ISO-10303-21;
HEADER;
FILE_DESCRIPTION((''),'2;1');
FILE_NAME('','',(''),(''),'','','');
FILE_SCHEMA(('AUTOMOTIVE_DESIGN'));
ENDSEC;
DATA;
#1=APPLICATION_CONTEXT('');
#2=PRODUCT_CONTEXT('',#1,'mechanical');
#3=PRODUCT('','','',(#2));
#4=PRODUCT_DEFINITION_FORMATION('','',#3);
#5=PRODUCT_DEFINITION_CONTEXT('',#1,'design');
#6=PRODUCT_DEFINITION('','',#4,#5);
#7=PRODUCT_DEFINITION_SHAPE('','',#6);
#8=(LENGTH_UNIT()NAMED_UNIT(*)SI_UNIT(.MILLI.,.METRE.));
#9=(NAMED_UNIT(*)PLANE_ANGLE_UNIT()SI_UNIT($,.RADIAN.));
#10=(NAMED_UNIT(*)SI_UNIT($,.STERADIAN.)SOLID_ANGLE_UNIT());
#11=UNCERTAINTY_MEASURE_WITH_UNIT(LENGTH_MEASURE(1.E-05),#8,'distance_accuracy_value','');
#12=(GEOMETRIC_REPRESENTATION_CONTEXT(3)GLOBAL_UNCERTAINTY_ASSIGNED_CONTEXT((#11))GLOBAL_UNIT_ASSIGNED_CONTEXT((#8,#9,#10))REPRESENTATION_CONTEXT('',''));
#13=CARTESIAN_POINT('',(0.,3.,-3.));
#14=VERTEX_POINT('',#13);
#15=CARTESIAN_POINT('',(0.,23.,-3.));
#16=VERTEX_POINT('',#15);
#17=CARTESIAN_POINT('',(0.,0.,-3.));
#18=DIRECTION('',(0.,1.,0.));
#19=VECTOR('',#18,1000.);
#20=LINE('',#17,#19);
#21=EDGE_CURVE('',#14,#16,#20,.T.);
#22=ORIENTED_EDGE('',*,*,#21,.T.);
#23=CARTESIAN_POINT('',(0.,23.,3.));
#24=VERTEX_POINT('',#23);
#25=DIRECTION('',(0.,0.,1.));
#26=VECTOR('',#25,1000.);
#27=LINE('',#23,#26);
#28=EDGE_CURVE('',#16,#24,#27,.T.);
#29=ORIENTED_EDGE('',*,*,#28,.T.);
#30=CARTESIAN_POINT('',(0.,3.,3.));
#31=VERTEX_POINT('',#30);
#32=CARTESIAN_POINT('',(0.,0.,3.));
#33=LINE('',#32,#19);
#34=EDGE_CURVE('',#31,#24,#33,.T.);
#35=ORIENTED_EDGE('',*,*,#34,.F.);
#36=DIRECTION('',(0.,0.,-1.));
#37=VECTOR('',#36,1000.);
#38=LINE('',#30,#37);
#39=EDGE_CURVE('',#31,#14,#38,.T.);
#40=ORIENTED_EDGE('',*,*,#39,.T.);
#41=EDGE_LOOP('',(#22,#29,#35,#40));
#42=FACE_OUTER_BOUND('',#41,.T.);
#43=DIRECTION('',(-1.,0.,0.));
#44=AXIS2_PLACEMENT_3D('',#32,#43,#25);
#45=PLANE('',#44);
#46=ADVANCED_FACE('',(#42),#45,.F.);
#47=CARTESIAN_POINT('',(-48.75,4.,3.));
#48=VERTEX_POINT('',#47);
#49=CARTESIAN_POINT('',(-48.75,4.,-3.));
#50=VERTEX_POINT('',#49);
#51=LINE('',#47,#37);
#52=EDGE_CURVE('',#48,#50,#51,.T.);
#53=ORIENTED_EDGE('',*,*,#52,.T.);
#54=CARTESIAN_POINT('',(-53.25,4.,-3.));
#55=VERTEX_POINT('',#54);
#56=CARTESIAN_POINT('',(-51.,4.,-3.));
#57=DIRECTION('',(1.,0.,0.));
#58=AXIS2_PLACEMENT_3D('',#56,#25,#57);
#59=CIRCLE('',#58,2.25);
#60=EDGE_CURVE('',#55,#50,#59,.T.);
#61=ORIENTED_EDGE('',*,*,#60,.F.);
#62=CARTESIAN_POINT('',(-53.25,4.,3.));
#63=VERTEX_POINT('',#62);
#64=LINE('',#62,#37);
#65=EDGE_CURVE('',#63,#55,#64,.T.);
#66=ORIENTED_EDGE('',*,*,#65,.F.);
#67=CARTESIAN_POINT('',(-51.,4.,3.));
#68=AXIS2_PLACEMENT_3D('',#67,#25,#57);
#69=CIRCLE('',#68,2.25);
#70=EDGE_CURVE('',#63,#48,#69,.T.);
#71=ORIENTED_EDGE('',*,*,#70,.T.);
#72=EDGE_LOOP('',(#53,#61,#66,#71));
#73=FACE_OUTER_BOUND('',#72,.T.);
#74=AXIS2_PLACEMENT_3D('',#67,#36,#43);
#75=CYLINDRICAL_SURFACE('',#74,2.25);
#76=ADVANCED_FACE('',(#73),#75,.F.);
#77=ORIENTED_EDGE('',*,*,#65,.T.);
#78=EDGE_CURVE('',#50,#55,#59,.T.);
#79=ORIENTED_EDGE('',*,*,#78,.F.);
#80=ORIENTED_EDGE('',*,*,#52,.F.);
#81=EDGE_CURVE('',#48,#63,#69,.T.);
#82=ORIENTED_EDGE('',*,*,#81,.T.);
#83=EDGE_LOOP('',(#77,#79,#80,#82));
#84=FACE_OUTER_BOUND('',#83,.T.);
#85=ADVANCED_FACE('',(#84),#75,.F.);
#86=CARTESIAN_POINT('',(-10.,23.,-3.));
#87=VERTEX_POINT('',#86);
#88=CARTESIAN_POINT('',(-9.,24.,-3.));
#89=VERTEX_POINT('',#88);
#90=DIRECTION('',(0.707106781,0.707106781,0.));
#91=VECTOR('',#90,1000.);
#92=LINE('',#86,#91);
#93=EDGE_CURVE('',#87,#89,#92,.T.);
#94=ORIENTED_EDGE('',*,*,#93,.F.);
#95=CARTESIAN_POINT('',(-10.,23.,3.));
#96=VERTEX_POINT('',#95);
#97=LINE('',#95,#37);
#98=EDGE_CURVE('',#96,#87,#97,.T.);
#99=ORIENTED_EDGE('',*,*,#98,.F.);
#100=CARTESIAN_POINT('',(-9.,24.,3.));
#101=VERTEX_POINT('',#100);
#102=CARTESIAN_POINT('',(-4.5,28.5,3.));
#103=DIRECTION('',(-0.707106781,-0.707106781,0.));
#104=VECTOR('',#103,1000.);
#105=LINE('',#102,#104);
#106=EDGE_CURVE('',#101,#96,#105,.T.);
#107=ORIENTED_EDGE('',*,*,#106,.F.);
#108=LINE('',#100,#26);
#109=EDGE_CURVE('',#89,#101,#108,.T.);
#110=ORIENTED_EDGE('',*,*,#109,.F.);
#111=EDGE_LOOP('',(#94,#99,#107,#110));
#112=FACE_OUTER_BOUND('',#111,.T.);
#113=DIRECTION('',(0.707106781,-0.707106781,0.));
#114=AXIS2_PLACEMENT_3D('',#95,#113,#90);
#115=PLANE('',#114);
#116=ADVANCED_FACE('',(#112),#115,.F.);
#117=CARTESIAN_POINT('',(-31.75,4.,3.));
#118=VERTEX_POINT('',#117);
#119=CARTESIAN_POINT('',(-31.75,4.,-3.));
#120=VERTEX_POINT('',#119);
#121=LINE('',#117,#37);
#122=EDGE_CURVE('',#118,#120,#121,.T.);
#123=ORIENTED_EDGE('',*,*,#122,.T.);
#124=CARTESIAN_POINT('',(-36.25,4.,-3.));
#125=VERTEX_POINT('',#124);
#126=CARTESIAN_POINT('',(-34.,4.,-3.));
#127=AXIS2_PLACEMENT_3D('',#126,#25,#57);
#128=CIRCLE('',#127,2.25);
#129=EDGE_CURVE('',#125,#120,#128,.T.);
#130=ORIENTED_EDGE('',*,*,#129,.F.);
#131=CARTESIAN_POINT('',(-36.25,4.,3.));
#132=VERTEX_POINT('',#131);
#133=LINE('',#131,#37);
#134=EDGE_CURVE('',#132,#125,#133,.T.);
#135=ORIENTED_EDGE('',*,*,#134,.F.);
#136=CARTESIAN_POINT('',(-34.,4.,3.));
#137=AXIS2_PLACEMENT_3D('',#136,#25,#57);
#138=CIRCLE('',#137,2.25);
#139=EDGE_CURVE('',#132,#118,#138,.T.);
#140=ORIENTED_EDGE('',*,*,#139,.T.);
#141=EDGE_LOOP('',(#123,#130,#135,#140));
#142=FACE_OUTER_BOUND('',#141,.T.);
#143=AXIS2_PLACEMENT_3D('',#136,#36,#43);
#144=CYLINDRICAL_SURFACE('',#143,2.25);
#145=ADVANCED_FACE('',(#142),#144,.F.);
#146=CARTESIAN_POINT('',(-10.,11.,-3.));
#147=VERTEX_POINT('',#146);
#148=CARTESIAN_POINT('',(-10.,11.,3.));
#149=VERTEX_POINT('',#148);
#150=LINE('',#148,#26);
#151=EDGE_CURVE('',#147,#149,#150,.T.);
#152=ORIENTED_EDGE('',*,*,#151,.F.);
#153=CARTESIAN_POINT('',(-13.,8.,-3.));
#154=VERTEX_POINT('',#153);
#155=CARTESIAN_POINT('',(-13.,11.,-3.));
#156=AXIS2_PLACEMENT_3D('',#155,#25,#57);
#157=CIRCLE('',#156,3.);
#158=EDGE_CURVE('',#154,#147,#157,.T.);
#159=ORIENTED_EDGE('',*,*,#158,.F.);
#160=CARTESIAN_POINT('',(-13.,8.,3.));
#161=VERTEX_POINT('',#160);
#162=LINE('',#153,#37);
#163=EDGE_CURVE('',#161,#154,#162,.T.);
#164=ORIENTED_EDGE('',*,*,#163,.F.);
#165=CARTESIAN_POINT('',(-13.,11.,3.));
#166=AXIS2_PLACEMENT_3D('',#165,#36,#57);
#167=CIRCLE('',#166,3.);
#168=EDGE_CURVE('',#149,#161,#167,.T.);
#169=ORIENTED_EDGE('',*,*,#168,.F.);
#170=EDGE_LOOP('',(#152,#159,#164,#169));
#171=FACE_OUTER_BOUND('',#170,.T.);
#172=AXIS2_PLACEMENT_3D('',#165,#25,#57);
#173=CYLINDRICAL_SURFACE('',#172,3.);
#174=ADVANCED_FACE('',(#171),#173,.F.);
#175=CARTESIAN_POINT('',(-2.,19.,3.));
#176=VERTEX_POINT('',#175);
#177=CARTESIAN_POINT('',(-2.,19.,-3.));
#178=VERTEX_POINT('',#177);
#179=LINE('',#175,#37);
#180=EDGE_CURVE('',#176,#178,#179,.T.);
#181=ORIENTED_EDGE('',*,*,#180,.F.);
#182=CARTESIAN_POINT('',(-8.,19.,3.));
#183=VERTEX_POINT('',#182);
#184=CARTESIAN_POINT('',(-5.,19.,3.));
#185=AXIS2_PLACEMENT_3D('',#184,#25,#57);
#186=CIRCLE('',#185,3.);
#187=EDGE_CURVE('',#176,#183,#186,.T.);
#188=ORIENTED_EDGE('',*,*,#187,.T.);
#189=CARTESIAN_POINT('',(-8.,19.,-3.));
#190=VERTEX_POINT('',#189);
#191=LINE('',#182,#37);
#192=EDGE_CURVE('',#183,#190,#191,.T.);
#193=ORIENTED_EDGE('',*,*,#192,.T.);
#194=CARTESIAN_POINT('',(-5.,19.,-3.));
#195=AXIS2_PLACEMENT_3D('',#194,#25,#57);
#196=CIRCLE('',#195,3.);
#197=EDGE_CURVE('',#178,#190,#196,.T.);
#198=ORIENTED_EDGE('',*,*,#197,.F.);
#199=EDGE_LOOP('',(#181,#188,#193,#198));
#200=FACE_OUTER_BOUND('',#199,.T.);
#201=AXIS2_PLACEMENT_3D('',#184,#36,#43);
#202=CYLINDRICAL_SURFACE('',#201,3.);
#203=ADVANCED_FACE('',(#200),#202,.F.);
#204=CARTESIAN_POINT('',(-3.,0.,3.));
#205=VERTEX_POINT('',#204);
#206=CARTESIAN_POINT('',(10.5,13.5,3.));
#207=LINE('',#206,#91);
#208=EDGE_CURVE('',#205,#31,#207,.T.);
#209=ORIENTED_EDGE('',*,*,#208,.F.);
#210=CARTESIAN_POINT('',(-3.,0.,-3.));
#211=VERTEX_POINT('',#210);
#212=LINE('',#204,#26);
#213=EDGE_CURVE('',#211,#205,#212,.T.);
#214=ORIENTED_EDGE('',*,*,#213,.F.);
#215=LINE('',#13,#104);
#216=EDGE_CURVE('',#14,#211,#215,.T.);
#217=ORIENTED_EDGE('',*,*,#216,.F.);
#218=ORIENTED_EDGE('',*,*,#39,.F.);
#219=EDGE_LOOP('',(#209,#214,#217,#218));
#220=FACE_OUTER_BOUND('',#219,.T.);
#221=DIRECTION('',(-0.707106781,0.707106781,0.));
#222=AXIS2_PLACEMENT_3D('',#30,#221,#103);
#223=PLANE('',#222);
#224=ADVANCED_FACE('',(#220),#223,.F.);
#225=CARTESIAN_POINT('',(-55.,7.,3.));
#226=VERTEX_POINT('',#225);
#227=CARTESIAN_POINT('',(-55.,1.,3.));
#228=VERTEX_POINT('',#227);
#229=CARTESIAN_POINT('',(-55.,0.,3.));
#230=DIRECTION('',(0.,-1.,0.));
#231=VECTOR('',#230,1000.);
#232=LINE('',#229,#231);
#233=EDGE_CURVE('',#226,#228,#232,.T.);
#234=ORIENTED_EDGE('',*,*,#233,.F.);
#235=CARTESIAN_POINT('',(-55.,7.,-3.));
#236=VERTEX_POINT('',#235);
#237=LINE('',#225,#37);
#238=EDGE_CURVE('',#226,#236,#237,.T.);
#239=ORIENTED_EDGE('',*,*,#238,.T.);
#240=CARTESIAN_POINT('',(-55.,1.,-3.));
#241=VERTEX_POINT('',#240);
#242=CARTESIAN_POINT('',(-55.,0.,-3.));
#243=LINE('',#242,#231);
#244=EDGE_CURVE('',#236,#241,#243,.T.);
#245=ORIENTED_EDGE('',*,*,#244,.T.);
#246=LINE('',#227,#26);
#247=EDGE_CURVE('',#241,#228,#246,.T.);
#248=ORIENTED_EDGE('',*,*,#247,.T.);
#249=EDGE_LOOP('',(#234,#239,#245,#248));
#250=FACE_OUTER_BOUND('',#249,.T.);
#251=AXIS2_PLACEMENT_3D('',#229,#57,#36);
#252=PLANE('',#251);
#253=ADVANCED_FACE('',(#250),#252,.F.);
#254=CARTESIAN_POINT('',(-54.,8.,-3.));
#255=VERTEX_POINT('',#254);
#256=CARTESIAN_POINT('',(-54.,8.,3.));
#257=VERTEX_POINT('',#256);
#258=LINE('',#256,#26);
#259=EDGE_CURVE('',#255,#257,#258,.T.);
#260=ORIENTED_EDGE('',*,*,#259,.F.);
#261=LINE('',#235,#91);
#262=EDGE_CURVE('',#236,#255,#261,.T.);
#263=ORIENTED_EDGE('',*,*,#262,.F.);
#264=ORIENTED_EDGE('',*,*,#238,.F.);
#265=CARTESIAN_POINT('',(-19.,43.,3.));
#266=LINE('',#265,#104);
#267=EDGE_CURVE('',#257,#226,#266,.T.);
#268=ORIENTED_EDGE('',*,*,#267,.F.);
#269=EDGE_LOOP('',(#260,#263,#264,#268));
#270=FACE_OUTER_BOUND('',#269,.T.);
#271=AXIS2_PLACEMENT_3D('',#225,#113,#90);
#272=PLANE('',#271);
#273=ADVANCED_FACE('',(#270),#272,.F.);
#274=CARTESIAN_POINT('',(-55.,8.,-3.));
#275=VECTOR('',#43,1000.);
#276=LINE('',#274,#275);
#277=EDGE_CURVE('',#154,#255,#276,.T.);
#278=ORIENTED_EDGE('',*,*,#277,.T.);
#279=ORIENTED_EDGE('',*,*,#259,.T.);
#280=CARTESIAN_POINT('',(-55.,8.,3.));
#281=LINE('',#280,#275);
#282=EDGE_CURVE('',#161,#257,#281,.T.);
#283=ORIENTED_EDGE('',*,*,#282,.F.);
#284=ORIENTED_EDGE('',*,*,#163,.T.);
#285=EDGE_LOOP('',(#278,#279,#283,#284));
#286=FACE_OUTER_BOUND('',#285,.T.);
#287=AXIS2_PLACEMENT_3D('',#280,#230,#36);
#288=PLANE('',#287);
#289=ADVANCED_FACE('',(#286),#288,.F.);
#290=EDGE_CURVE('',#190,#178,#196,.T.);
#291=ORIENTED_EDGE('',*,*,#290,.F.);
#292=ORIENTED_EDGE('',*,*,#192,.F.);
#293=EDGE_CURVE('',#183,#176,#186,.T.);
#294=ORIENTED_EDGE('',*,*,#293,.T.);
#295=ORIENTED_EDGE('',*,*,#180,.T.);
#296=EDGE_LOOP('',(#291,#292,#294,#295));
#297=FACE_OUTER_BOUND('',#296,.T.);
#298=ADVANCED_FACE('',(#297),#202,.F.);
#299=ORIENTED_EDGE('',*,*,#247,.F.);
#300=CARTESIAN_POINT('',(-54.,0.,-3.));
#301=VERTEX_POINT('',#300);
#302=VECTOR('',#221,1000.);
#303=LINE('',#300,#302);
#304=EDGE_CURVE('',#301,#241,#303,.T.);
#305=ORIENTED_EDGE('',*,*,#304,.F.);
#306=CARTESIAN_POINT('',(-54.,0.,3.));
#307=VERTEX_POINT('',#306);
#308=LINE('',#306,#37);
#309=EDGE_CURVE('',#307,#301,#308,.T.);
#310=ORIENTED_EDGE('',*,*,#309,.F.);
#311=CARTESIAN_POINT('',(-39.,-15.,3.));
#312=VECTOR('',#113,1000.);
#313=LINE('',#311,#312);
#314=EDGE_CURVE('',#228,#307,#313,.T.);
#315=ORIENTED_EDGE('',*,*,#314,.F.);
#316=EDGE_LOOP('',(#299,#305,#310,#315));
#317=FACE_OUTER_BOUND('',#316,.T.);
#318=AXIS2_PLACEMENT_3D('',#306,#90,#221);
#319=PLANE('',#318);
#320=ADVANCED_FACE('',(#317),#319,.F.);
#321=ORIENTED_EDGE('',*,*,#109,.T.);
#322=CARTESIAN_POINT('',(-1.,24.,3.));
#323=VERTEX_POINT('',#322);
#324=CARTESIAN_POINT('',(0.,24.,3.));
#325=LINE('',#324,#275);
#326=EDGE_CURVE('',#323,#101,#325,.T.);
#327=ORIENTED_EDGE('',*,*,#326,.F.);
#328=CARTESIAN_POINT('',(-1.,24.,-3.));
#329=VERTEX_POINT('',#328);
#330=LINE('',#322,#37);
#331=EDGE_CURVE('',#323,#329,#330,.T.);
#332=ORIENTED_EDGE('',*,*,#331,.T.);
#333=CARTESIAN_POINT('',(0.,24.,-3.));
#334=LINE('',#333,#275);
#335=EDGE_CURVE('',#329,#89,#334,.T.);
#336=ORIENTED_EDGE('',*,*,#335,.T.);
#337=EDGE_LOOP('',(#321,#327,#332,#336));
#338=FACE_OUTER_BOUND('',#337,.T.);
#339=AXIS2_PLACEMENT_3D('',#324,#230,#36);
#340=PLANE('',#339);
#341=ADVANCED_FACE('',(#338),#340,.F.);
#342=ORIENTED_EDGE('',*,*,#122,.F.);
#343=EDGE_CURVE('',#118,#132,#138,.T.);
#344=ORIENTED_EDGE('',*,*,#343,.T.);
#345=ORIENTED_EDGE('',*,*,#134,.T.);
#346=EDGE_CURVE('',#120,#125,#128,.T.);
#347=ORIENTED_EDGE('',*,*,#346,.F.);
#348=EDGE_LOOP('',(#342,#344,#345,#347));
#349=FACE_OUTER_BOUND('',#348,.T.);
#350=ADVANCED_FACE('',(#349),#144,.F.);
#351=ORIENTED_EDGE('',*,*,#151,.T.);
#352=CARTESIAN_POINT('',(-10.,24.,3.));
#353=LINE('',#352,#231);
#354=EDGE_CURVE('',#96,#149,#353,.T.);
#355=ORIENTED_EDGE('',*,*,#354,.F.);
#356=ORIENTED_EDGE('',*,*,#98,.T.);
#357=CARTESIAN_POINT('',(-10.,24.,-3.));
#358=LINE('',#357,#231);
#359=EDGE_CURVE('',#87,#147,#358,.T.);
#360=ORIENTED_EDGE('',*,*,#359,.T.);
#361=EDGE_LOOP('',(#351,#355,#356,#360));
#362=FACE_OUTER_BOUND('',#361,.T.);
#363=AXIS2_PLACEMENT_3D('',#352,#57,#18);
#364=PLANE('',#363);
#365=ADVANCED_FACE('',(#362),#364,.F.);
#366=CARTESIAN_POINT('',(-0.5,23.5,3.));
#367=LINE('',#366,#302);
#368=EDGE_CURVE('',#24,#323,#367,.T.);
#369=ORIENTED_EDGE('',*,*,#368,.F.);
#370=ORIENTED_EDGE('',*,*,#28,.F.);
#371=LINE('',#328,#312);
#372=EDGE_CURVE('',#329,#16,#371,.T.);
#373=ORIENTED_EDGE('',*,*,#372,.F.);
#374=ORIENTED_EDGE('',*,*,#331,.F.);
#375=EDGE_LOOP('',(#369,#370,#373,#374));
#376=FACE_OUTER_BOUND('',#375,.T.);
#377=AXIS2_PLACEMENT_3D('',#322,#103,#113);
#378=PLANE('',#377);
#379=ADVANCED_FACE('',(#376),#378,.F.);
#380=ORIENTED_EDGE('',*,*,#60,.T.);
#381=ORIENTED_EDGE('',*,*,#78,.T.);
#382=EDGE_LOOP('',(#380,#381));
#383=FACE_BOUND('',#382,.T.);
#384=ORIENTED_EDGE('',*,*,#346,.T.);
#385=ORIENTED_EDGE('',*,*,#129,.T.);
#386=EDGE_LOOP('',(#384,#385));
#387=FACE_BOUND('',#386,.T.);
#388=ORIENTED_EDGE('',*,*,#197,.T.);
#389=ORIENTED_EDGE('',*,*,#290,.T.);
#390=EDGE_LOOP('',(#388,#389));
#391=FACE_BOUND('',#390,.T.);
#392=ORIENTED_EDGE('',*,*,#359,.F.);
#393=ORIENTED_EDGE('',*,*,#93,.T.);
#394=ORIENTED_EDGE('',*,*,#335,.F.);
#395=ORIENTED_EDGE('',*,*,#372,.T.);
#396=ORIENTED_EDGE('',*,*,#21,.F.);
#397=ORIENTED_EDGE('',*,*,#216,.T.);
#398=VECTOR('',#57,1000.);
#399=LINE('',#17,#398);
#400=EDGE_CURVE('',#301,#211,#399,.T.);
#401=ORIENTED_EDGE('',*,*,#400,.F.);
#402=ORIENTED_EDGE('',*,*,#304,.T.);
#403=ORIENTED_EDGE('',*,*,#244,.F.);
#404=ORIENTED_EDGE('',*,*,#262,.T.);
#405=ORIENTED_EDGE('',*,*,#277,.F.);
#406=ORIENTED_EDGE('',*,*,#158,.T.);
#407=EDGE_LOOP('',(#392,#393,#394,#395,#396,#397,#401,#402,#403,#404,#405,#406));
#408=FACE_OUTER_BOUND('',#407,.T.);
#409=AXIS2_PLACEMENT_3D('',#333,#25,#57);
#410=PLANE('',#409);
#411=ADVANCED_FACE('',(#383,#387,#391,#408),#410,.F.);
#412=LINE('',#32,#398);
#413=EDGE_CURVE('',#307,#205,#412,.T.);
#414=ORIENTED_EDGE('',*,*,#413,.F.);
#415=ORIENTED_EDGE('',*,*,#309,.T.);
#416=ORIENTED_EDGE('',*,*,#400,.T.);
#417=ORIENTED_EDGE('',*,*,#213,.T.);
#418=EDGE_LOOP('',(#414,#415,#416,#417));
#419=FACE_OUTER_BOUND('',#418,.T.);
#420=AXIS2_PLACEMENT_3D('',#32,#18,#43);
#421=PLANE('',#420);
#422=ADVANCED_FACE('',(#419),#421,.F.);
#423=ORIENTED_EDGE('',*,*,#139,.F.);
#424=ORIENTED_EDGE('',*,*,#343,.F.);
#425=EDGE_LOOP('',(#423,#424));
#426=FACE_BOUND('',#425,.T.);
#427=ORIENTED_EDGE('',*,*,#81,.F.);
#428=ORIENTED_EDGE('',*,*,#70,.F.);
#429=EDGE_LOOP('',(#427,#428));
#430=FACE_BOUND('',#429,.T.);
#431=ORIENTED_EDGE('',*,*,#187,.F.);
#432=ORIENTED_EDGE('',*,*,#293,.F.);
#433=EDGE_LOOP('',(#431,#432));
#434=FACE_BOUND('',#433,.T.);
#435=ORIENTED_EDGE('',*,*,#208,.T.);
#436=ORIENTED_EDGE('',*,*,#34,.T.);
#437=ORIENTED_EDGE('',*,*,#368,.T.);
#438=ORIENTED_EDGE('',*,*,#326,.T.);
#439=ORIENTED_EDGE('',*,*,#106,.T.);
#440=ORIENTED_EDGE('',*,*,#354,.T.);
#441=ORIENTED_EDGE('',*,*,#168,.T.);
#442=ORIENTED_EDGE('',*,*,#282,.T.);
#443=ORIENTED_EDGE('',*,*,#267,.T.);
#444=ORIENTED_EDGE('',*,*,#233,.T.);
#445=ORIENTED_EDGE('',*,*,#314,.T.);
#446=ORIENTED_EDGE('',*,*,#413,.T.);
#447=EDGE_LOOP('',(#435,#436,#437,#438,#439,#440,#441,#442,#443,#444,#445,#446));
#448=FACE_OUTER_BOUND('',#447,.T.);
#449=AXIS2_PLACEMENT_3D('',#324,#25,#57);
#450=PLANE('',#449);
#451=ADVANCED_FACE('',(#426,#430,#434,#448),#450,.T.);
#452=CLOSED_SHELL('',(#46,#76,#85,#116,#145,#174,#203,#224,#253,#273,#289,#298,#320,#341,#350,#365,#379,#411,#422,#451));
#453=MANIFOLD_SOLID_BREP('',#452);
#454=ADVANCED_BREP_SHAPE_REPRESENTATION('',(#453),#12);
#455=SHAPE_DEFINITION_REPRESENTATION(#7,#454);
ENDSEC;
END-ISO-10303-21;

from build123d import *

# Parameters (mm, degrees)
SKETCH1_R           = 2.25
SKETCH1_R_2         = 3
BOSS_EXTRUDE1_DEPTH = 3
FILLET1_R           = 3
CHAMFER1_SIZE       = 3
CHAMFER2_SIZE       = 1


with BuildPart() as part:
    # Sketch1 → Boss-Extrude1 (new, symmetric)
    with BuildSketch(Plane.XY):
        Polygon((0, 0), (-55, 0), (-55, 8), (-10, 8), (-10, 24), (0, 24), align=None)
        with Locations((-51, 4)):
            Circle(SKETCH1_R, mode=Mode.SUBTRACT)
        with Locations((-34, 4)):
            Circle(SKETCH1_R, mode=Mode.SUBTRACT)
        with Locations((-5, 19)):
            Circle(SKETCH1_R_2, mode=Mode.SUBTRACT)
    extrude(amount=BOSS_EXTRUDE1_DEPTH, both=True)

    # Fillet1
    fillet1_edges = [part.edges().sort_by_distance(p)[0] for p in [
        (-10, 8, 0),
    ]]
    fillet(fillet1_edges, radius=FILLET1_R)

    # Chamfer1
    chamfer1_edges = [part.edges().sort_by_distance(p)[0] for p in [
        (0, 0, 0),
    ]]
    chamfer(chamfer1_edges, length=CHAMFER1_SIZE)

    # Chamfer2
    chamfer2_edges = [part.edges().sort_by_distance(p)[0] for p in [
        (-55, 0, 0),
        (-55, 8, 0),
        (-10, 24, 0),
        (0, 24, 0),
    ]]
    chamfer(chamfer2_edges, length=CHAMFER2_SIZE)


solid = part.part
